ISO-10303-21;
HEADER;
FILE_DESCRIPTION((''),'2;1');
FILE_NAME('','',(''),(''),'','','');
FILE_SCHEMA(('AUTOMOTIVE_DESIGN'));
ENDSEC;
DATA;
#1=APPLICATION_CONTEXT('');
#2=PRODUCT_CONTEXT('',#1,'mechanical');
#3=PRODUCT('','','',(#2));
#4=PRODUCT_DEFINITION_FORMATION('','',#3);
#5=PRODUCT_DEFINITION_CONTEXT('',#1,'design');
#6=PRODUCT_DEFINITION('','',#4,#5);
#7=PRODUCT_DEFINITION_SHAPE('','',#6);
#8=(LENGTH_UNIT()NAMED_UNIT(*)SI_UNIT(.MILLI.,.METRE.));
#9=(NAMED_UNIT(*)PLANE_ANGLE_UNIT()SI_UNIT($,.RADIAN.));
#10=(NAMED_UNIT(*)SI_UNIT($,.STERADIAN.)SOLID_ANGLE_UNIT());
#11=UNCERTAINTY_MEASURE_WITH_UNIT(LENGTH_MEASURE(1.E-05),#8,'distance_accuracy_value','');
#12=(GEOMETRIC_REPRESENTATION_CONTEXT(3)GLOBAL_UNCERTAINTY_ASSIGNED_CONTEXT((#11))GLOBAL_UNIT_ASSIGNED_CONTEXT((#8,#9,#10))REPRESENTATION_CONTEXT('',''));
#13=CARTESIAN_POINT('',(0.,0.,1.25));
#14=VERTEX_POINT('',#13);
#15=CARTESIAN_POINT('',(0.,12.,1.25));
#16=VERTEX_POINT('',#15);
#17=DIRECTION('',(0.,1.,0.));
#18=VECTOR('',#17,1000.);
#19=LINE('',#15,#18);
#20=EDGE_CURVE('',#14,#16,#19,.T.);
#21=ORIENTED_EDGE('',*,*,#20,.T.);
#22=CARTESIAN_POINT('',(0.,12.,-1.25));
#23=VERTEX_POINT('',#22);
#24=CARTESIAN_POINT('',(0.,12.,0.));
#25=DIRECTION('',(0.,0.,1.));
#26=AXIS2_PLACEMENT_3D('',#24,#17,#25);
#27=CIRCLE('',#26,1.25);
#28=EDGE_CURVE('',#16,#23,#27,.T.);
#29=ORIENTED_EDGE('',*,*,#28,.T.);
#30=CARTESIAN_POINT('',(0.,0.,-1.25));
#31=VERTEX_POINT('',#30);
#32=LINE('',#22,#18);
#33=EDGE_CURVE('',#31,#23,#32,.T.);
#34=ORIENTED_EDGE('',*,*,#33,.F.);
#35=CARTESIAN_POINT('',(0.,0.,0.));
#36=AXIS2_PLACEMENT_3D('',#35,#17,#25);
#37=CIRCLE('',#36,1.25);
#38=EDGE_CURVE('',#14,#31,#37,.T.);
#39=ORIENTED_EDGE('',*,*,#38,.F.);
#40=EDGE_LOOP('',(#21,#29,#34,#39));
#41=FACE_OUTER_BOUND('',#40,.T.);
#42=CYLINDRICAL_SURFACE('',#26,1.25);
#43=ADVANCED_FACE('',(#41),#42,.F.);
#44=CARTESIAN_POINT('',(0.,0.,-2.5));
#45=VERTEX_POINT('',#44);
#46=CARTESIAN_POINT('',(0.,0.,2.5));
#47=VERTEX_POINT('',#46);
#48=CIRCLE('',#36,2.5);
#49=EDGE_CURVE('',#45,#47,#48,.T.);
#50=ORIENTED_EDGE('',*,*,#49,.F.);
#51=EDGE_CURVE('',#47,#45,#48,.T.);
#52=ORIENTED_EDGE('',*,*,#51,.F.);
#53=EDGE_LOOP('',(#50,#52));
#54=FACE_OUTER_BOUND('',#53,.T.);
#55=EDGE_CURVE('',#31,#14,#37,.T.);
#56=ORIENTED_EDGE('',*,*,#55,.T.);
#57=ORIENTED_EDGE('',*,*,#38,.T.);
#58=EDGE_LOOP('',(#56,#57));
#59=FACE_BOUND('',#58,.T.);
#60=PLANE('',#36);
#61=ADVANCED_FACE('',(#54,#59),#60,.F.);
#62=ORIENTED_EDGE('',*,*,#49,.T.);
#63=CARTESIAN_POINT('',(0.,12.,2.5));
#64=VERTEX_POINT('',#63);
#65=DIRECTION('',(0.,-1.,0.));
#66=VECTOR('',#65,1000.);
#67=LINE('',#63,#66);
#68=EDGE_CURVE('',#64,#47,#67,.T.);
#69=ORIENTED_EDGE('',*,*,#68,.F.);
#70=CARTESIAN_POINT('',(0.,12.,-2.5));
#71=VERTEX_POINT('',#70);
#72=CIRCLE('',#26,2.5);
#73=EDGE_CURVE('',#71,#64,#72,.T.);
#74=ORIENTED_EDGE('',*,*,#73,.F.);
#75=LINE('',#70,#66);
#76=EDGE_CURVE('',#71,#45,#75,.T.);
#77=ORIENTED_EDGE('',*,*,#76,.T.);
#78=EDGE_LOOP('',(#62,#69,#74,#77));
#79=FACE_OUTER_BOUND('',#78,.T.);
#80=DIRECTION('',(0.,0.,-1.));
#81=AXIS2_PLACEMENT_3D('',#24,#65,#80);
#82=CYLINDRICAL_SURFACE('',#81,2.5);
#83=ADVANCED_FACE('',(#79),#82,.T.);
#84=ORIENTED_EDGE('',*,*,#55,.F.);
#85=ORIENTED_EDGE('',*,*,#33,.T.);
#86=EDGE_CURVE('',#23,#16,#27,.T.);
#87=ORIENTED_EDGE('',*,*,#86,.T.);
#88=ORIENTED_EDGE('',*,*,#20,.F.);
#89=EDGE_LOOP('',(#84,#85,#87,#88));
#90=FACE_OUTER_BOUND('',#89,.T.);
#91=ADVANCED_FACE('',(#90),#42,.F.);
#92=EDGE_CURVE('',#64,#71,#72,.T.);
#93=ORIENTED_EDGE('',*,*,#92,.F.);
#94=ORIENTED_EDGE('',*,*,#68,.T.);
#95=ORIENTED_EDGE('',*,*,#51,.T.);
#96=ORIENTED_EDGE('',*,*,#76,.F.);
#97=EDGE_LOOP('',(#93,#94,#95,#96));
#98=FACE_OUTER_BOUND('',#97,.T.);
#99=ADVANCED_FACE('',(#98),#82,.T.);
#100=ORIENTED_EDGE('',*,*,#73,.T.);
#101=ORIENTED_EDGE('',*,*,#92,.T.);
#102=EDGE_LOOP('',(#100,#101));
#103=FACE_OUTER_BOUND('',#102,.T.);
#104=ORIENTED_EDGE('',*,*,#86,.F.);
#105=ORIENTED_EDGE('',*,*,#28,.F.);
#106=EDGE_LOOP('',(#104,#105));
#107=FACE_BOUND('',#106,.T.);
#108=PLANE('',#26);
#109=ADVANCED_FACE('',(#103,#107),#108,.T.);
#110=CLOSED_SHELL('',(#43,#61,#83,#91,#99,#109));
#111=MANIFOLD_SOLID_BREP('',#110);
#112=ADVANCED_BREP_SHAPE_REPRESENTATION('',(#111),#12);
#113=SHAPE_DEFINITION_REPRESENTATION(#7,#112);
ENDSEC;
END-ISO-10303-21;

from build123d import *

# Parameters (mm, degrees)
SKETCH_1_R         = 2.5
EXTRUDE_1_DEPTH    = 12
HOLE_WIZARD_M3_1_D = 2.5


with BuildPart() as part:
    # 草图1 → 凸台-拉伸1 (new body)
    with BuildSketch(Plane(origin=(0, 0, 0), x_dir=(1, 0, 0), z_dir=(0, 1, 0))):
        with Locations(Location((0, 0, 0), (0, 0, 270))):
            Circle(SKETCH_1_R)
    extrude(amount=EXTRUDE_1_DEPTH)

    # M3 螺纹孔1 (through all)
    with Locations(Plane(origin=(0, 12, 0), x_dir=(1, 0, 0), z_dir=(0, 1, 0))):
        with Locations((0, 0)):
            Hole(HOLE_WIZARD_M3_1_D / 2)


solid = part.part
